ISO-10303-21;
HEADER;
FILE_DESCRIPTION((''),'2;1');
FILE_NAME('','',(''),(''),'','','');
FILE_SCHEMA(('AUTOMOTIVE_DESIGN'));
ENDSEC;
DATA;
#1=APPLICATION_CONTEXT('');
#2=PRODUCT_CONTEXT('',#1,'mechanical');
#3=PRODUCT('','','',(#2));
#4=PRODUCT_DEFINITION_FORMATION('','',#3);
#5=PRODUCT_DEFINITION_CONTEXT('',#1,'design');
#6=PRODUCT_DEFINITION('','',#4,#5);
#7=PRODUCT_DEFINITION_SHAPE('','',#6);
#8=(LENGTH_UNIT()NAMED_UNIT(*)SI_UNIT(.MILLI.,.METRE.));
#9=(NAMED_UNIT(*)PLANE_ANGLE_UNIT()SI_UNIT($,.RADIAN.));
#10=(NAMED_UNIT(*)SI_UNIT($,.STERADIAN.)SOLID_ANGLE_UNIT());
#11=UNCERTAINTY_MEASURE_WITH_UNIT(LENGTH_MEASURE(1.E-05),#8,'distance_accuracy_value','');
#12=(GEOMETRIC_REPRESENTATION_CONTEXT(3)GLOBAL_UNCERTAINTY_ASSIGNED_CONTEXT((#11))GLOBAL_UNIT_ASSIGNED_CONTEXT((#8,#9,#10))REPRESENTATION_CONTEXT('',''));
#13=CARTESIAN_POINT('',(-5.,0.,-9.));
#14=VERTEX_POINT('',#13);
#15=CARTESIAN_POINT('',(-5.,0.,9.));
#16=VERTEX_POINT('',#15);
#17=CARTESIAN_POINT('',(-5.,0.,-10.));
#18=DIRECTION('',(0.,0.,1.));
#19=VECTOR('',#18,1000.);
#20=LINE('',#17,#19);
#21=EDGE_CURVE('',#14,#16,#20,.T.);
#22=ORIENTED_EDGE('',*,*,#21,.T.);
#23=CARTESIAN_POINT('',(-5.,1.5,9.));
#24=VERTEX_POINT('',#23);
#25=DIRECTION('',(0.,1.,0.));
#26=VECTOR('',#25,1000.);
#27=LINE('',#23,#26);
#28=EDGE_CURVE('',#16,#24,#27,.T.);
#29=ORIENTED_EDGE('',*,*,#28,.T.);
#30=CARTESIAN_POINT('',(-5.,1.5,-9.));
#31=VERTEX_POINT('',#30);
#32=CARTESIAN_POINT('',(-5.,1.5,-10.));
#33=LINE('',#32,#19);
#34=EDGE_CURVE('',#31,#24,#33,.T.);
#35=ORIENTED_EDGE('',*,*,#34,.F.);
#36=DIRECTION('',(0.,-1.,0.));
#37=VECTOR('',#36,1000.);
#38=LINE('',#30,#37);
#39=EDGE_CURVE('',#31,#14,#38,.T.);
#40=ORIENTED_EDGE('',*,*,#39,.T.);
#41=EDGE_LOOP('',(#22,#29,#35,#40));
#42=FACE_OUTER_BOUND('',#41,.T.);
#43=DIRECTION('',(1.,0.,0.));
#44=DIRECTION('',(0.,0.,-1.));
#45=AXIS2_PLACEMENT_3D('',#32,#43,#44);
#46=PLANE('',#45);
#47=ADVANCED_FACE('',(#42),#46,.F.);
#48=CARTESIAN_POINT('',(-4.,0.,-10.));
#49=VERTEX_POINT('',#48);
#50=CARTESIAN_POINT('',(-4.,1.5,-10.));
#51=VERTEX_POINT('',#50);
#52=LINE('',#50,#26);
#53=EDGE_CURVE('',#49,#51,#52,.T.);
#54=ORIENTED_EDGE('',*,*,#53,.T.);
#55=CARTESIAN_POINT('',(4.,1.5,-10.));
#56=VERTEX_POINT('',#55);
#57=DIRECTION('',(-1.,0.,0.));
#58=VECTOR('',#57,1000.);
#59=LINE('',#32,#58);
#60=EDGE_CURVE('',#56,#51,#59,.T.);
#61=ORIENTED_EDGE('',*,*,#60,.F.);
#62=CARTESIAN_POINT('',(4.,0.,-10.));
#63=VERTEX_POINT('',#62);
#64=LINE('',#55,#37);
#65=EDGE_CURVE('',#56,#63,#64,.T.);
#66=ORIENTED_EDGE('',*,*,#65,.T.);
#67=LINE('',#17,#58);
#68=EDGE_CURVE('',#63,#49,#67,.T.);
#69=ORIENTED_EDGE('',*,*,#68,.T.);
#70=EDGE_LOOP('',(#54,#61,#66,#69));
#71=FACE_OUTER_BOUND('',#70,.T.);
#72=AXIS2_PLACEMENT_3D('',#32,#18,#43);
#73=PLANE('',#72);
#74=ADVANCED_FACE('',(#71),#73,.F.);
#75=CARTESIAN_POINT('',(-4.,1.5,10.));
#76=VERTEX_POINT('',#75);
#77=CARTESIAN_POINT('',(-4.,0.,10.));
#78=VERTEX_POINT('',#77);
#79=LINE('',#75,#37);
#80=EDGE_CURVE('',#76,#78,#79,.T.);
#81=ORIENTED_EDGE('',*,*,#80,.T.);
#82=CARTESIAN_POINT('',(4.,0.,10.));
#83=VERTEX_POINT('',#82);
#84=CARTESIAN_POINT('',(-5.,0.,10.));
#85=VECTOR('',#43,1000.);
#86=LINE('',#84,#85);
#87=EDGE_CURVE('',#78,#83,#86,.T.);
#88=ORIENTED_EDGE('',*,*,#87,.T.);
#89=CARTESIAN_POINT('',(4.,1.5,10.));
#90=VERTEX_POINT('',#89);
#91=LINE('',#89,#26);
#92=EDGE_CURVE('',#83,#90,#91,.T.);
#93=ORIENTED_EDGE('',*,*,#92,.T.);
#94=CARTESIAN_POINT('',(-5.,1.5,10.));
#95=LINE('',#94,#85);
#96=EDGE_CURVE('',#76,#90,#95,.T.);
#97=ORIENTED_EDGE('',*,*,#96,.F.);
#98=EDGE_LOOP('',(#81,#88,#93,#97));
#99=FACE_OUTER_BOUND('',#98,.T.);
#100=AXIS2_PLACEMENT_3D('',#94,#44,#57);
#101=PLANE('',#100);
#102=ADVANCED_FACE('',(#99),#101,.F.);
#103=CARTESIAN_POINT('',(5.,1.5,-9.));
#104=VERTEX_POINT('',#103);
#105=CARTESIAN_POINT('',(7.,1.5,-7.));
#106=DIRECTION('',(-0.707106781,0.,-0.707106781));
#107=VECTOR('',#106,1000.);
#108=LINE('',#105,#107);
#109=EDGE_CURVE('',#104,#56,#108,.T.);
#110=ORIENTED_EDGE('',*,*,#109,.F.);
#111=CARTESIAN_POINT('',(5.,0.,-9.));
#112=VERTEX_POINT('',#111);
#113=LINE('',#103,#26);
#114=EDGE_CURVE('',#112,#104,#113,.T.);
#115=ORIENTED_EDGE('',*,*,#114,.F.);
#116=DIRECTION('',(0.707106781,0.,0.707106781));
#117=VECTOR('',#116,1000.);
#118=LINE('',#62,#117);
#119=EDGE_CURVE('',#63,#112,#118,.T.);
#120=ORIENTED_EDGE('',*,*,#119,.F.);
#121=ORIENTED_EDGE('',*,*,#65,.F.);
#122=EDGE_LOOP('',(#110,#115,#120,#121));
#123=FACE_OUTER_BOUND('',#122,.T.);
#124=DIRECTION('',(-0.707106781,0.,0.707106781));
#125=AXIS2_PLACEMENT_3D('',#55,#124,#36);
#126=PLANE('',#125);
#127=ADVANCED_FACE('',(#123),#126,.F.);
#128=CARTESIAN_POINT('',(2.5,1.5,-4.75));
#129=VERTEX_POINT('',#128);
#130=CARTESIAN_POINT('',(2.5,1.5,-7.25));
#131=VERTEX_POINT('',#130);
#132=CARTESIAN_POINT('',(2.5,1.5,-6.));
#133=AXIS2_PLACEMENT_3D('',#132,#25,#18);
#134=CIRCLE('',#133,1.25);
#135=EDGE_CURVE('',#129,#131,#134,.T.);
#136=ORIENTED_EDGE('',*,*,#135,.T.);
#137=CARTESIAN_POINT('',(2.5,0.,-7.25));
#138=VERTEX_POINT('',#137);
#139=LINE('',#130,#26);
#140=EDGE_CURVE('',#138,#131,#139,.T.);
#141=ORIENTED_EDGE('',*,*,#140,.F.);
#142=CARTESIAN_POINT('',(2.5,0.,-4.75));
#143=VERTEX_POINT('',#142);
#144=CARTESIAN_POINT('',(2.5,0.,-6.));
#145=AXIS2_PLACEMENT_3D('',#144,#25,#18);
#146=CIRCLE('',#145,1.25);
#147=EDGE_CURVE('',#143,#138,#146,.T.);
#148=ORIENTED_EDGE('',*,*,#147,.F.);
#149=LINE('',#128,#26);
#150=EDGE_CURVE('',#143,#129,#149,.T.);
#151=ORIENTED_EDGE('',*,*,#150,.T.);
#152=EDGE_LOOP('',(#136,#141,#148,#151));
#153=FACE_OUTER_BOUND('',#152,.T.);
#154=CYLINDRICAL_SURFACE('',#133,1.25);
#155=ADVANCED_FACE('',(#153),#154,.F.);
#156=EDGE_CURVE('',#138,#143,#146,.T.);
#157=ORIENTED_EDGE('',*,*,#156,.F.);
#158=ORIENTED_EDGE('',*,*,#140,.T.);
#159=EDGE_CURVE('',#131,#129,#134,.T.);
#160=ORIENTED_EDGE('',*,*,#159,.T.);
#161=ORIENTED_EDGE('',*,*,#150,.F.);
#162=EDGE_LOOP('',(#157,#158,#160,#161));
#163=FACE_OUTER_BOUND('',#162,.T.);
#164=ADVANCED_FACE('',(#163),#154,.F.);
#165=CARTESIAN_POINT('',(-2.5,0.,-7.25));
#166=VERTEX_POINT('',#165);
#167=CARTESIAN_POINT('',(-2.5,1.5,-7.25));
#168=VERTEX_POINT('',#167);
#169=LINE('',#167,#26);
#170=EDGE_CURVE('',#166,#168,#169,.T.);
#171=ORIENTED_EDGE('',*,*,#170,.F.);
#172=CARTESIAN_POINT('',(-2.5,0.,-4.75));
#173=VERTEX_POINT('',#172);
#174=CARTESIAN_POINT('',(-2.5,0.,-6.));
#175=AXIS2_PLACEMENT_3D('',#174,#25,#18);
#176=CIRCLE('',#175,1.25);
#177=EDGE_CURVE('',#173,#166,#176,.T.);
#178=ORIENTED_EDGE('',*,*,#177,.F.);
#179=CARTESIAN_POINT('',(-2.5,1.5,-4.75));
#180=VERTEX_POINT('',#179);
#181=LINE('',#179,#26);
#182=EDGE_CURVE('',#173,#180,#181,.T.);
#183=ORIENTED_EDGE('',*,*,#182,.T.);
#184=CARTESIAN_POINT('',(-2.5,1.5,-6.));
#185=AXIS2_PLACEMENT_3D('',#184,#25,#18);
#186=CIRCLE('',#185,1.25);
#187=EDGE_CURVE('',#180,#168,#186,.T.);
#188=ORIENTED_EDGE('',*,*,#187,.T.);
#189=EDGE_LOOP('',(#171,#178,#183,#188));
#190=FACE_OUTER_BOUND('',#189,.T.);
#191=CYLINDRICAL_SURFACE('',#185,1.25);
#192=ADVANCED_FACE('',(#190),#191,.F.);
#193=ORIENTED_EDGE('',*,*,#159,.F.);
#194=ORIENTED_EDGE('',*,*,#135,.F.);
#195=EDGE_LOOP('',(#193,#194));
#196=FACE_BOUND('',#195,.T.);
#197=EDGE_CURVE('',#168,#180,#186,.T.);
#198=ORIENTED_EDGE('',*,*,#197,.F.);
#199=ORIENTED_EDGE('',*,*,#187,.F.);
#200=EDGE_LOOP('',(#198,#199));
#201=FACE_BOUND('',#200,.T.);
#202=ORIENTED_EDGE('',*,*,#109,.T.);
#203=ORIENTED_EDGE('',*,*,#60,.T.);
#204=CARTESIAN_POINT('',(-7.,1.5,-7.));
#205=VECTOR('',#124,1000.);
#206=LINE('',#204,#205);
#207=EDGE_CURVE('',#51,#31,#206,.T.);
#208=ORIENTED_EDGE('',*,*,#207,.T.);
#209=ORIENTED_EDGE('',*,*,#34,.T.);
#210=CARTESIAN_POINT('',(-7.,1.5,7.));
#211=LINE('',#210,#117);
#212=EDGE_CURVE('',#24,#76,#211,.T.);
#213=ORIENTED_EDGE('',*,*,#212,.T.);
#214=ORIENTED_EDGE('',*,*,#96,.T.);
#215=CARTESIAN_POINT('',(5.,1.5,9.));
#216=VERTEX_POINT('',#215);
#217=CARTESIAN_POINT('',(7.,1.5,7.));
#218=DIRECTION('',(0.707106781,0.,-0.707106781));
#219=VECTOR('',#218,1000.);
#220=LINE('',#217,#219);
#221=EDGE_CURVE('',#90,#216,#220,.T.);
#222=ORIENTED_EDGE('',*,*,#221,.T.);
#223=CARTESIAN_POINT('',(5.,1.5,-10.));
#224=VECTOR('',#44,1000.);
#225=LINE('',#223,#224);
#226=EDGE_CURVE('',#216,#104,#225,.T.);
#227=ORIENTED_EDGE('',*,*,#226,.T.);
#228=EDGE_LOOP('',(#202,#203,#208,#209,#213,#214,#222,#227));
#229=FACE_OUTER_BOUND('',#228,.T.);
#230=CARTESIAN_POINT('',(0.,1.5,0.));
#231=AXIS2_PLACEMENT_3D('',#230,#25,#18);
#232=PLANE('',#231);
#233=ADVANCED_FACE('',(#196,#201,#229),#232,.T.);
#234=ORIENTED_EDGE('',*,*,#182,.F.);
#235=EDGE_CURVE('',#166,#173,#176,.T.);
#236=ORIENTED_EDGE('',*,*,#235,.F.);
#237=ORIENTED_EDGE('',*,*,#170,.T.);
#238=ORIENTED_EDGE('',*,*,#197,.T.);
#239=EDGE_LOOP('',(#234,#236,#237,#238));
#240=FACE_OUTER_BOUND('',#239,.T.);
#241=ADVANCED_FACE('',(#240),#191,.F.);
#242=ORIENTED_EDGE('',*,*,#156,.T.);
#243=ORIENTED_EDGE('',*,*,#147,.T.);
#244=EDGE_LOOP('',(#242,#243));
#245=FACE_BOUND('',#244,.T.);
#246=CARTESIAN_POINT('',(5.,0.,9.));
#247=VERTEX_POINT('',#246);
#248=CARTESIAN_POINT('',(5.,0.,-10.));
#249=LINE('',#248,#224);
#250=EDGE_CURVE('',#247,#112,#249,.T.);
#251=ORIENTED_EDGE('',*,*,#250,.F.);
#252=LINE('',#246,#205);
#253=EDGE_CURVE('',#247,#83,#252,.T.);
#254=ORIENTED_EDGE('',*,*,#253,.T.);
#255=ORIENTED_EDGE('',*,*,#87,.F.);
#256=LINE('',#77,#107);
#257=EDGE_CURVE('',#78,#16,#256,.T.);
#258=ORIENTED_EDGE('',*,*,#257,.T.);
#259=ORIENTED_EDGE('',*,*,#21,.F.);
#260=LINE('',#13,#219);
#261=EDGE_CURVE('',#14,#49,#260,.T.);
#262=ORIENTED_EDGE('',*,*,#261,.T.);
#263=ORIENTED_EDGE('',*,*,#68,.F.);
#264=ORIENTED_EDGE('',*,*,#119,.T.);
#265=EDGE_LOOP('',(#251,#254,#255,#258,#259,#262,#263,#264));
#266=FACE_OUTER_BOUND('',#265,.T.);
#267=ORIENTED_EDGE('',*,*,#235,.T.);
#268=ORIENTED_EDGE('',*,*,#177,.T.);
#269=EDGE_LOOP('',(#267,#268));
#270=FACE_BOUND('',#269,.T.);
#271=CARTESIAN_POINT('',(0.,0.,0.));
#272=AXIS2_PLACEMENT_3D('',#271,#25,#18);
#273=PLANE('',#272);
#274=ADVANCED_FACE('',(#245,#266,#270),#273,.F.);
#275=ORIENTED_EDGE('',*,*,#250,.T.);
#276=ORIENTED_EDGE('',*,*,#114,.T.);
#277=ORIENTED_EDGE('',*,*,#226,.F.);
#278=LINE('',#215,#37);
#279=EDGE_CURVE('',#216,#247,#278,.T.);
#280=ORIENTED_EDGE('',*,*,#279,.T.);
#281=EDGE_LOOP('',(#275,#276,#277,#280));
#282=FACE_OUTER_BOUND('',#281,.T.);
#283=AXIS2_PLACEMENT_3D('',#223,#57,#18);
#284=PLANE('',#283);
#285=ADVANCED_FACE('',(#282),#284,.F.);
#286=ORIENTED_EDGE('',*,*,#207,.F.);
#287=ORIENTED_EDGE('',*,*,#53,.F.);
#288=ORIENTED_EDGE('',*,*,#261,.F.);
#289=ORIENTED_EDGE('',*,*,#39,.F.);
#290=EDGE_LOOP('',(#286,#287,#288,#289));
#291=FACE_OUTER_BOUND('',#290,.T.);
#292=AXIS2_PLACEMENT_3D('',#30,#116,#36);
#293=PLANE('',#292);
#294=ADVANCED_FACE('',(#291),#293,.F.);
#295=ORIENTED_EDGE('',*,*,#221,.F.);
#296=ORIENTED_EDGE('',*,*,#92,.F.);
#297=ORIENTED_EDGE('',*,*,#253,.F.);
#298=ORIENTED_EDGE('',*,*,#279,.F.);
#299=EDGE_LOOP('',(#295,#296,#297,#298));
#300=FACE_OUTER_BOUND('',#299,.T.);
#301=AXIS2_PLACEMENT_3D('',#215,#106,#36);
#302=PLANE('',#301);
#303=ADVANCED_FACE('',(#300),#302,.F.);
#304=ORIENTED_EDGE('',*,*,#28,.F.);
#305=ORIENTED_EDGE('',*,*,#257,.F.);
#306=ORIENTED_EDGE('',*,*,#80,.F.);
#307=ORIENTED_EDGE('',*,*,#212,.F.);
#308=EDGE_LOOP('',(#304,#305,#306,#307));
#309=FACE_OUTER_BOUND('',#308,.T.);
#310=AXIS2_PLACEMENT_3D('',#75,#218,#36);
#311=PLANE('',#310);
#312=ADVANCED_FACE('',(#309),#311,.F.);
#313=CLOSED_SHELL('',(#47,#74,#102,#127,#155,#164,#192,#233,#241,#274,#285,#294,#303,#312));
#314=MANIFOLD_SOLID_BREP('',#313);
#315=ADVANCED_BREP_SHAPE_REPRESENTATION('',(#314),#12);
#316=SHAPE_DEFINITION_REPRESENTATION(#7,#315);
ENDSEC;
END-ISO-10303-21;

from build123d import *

# Parameters (mm, degrees)
SKETCH1_W                      = 10
SKETCH1_H                      = 20
BOSS_EXTRUDE1_DEPTH            = 1.5
CHAMFER1_SIZE                  = 1
F_2_5_2_5_DIAMETER_HOLE1_D     = 2.5
F_2_5_2_5_DIAMETER_HOLE1_DEPTH = 10
F_2_5_2_5_DIAMETER_HOLE1_TIP   = 0.751075774


with BuildPart() as part:
    # Sketch1 → Boss-Extrude1 (new body)
    with BuildSketch(Plane(origin=(0, 0, 0), x_dir=(1, 0, 0), z_dir=(0, 1, 0))):
        Rectangle(SKETCH1_W, SKETCH1_H)
    extrude(amount=BOSS_EXTRUDE1_DEPTH)

    # Chamfer1
    chamfer1_edges = [part.edges().sort_by_distance(p)[0] for p in [
        (5, 0.75, 10),
        (-5, 0.75, 10),
        (-5, 0.75, -10),
        (5, 0.75, -10),
    ]]
    chamfer(chamfer1_edges, length=CHAMFER1_SIZE)

    # Ø2.5 (2.5) Diameter Hole1
    with Locations(Plane(origin=(-2.5, 1.5, -6), x_dir=(0, 0, 1), z_dir=(0, 1, 0))):
        with Locations((0, 0), (0, 5)):
            Hole(F_2_5_2_5_DIAMETER_HOLE1_D / 2, depth=F_2_5_2_5_DIAMETER_HOLE1_DEPTH)
            with Locations((0, 0, -(F_2_5_2_5_DIAMETER_HOLE1_DEPTH + F_2_5_2_5_DIAMETER_HOLE1_TIP / 2))):  # 118° drill point
                Cone(0, F_2_5_2_5_DIAMETER_HOLE1_D / 2, F_2_5_2_5_DIAMETER_HOLE1_TIP, mode=Mode.SUBTRACT)


solid = part.part
